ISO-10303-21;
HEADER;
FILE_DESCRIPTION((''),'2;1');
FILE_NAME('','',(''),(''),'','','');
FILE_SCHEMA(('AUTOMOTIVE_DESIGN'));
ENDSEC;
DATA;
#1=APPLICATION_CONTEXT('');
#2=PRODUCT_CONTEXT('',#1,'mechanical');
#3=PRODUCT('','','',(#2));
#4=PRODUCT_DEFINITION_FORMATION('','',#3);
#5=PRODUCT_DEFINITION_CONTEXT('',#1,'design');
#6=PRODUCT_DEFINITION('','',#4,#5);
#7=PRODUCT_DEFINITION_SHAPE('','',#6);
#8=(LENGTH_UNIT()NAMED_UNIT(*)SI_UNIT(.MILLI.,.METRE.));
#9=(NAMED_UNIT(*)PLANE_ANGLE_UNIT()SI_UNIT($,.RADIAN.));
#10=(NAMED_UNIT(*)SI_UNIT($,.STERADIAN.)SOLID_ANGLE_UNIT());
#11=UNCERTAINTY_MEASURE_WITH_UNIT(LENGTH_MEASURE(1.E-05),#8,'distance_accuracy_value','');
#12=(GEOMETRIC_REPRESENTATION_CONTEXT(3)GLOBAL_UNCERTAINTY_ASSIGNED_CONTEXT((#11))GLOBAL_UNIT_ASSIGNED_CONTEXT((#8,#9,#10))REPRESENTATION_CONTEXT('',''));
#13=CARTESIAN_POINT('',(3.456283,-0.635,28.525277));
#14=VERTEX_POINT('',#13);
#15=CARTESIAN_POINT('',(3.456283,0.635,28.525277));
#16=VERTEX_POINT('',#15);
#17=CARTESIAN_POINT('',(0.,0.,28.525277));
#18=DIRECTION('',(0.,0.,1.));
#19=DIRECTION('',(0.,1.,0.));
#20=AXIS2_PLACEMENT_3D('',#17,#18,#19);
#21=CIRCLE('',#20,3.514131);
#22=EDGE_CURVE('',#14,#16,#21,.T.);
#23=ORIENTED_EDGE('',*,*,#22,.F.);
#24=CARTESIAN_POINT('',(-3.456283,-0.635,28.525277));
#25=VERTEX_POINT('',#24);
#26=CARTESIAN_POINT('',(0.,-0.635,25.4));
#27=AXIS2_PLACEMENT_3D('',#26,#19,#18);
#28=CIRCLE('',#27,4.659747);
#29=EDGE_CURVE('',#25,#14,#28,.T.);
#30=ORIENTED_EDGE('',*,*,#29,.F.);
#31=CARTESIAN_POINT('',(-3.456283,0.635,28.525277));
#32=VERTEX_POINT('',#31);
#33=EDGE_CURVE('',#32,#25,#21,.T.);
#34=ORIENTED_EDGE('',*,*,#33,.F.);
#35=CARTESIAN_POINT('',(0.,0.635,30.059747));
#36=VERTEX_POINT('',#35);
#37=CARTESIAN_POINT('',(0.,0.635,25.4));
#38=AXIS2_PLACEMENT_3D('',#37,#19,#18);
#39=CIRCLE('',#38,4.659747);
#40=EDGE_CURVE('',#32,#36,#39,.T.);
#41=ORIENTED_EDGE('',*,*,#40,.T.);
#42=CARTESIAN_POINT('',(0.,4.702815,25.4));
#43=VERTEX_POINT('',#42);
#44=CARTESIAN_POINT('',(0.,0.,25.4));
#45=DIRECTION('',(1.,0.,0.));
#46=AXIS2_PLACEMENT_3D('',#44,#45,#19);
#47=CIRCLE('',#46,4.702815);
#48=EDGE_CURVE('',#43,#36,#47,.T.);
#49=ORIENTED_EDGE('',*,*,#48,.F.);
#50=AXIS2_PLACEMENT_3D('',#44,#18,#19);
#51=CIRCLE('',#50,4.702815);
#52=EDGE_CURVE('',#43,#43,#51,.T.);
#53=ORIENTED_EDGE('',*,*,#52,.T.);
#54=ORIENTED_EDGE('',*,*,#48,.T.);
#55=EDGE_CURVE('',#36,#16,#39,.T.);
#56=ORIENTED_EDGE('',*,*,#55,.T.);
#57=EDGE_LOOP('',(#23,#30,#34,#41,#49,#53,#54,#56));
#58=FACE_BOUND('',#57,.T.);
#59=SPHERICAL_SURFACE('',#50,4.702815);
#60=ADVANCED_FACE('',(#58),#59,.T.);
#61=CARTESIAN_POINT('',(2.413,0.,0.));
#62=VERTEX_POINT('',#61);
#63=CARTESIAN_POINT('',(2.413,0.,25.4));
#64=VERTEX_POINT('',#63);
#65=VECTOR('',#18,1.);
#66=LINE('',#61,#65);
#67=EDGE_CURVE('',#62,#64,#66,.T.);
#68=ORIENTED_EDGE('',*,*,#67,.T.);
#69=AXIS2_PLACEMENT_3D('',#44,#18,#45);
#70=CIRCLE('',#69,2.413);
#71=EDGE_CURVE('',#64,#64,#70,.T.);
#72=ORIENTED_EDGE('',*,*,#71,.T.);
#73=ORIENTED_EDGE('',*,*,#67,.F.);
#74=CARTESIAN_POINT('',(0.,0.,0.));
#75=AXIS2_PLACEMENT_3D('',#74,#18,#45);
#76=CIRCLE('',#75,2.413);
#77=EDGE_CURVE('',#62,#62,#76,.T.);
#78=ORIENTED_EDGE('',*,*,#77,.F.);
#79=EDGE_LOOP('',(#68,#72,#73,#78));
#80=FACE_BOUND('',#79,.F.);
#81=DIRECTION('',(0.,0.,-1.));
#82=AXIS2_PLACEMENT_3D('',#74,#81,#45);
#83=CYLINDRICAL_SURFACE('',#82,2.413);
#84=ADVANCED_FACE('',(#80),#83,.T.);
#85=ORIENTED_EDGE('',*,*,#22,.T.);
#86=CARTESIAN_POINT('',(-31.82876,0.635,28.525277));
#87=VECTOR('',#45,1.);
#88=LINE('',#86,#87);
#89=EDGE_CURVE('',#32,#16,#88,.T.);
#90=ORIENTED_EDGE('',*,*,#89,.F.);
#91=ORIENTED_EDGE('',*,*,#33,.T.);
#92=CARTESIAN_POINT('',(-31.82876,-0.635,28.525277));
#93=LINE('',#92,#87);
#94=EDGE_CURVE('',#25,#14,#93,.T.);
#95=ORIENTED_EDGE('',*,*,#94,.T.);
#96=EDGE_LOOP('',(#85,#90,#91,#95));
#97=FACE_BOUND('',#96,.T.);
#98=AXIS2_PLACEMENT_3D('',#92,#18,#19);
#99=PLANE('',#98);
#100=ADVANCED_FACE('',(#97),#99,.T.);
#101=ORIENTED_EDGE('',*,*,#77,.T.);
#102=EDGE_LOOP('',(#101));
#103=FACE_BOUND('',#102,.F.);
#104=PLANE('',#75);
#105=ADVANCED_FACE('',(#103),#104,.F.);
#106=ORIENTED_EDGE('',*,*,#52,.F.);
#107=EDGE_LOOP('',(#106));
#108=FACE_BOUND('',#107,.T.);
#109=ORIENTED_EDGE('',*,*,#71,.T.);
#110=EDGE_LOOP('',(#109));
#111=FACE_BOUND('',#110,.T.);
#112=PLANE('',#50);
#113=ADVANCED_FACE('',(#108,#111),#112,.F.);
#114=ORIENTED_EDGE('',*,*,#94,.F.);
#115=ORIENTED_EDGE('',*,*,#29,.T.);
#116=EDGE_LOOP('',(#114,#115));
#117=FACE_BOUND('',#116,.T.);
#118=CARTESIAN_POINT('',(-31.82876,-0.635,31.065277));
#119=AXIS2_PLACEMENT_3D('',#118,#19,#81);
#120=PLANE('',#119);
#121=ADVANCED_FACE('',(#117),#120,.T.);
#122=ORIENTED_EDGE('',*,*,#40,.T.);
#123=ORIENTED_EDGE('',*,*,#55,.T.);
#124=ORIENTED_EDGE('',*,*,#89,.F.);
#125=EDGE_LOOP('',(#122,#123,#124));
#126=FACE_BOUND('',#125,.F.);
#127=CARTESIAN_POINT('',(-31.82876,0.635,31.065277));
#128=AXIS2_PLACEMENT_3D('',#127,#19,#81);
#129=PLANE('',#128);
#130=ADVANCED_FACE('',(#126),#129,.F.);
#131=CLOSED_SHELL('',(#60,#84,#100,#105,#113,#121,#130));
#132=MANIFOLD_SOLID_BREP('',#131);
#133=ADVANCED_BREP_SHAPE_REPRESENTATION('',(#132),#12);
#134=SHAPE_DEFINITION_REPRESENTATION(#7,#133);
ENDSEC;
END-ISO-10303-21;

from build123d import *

# Parameters (mm, degrees)
SHANK_PROFILE_0_19_R        = 2.413
SHANK_DEPTH                 = 25.4
SCREWDRIVER_SLOT_DEPTH      = 31.828759505
SCREWDRIVER_SLOT_DEPTH_BACK = 31.828759505
SCREWDRIVER_SLOT_PROFILE_W  = 2.54
SCREWDRIVER_SLOT_PROFILE_H  = 1.27


with BuildPart() as part:
    # Shank Profile Ø0.19 → Shank (new body)
    with BuildSketch(Plane.XY):
        Circle(SHANK_PROFILE_0_19_R)
    extrude(amount=SHANK_DEPTH)

    # Round Head Profile → Round Head (revolve)
    with BuildSketch(Plane(origin=(0, 0, 0), x_dir=(0, 0, -1), z_dir=(1, 0, 0))):
        with BuildLine():
            Line((-25.4, 0), (-25.4, 4.702815049))
            ThreePointArc((-25.4, 4.702815049), (-28.725392412, 3.325392412), (-30.102815049, 0))
            Line((-30.102815049, 0), (-25.4, 0))
        make_face()
    revolve(axis=Axis((0, 0, 25.4), (0, 0, 1)))

    # Screwdriver Slot Profile → Screwdriver Slot (cut, two sides: drawn at the far end of the back side and taken through both)
    with BuildSketch(Plane(origin=(0, 0, 0), x_dir=(0, 0, -1), z_dir=(1, 0, 0)).offset(-SCREWDRIVER_SLOT_DEPTH_BACK)):
        with Locations((-29.795276549, 0)):
            Rectangle(SCREWDRIVER_SLOT_PROFILE_W, SCREWDRIVER_SLOT_PROFILE_H)
    extrude(amount=SCREWDRIVER_SLOT_DEPTH + SCREWDRIVER_SLOT_DEPTH_BACK, mode=Mode.SUBTRACT)


solid = part.part
